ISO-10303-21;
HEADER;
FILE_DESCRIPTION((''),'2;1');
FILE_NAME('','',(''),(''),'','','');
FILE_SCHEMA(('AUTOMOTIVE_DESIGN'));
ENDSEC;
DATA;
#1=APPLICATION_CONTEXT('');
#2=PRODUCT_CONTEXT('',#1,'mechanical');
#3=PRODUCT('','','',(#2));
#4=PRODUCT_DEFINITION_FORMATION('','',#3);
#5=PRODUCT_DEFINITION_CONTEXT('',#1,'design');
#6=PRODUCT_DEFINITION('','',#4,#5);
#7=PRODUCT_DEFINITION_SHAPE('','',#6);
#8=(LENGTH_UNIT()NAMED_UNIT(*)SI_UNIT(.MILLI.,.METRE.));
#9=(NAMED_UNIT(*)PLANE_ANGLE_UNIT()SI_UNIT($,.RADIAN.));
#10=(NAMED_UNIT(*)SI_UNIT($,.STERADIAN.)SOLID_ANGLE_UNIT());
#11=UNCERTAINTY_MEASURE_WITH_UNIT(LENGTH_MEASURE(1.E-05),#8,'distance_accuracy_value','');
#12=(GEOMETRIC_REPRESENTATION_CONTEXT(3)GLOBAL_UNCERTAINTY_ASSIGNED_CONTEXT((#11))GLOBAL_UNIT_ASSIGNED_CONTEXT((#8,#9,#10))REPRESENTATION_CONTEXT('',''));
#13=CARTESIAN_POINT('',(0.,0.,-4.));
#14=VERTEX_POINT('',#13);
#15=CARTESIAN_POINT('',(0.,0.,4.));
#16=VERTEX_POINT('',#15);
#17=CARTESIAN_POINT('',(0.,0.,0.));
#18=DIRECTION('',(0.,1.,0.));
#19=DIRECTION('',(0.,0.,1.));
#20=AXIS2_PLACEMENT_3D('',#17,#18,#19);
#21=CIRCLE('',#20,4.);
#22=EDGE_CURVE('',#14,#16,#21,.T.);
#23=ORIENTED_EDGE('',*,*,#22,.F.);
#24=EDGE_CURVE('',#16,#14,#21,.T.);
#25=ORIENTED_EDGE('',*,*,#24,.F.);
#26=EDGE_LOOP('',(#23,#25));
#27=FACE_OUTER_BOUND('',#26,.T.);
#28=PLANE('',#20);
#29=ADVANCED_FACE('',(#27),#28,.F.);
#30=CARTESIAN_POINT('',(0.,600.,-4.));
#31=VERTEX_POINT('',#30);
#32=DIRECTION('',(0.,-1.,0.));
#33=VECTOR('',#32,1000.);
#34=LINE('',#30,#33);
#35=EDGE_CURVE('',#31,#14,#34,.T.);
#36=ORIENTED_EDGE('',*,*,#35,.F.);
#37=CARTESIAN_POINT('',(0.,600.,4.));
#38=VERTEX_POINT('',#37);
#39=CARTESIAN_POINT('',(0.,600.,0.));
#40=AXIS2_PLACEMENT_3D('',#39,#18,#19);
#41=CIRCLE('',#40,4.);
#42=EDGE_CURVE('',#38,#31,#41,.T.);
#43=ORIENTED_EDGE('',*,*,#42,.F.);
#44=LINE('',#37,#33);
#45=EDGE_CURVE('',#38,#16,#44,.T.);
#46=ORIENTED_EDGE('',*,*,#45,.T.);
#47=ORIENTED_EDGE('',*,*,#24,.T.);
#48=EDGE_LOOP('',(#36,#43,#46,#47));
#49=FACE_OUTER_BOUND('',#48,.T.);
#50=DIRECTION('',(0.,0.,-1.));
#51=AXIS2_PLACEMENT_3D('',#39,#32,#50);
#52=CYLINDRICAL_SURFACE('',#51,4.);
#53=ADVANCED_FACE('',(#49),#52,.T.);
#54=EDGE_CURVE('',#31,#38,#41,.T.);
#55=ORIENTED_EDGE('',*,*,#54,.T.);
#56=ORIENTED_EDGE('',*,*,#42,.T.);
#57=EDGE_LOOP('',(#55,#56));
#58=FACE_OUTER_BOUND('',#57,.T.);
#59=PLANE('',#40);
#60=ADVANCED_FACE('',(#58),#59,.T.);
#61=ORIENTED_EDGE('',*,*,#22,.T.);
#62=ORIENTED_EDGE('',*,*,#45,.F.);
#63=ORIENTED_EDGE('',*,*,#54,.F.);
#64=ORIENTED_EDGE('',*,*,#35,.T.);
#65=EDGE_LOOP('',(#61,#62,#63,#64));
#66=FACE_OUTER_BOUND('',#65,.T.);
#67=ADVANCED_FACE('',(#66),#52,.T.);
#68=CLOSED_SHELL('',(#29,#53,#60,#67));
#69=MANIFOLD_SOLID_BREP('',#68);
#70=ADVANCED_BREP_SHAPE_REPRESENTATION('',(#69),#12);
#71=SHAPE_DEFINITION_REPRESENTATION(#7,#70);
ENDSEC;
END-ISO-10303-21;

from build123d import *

# Parameters (mm, degrees)
SKETCH1_R           = 4
BOSS_EXTRUDE1_DEPTH = 600


with BuildPart() as part:
    # Sketch1 → Boss-Extrude1 (new body)
    with BuildSketch(Plane(origin=(0, 0, 0), x_dir=(1, 0, 0), z_dir=(0, 1, 0))):
        with Locations(Location((0, 0, 0), (0, 0, 270))):
            Circle(SKETCH1_R)
    extrude(amount=BOSS_EXTRUDE1_DEPTH)


solid = part.part
